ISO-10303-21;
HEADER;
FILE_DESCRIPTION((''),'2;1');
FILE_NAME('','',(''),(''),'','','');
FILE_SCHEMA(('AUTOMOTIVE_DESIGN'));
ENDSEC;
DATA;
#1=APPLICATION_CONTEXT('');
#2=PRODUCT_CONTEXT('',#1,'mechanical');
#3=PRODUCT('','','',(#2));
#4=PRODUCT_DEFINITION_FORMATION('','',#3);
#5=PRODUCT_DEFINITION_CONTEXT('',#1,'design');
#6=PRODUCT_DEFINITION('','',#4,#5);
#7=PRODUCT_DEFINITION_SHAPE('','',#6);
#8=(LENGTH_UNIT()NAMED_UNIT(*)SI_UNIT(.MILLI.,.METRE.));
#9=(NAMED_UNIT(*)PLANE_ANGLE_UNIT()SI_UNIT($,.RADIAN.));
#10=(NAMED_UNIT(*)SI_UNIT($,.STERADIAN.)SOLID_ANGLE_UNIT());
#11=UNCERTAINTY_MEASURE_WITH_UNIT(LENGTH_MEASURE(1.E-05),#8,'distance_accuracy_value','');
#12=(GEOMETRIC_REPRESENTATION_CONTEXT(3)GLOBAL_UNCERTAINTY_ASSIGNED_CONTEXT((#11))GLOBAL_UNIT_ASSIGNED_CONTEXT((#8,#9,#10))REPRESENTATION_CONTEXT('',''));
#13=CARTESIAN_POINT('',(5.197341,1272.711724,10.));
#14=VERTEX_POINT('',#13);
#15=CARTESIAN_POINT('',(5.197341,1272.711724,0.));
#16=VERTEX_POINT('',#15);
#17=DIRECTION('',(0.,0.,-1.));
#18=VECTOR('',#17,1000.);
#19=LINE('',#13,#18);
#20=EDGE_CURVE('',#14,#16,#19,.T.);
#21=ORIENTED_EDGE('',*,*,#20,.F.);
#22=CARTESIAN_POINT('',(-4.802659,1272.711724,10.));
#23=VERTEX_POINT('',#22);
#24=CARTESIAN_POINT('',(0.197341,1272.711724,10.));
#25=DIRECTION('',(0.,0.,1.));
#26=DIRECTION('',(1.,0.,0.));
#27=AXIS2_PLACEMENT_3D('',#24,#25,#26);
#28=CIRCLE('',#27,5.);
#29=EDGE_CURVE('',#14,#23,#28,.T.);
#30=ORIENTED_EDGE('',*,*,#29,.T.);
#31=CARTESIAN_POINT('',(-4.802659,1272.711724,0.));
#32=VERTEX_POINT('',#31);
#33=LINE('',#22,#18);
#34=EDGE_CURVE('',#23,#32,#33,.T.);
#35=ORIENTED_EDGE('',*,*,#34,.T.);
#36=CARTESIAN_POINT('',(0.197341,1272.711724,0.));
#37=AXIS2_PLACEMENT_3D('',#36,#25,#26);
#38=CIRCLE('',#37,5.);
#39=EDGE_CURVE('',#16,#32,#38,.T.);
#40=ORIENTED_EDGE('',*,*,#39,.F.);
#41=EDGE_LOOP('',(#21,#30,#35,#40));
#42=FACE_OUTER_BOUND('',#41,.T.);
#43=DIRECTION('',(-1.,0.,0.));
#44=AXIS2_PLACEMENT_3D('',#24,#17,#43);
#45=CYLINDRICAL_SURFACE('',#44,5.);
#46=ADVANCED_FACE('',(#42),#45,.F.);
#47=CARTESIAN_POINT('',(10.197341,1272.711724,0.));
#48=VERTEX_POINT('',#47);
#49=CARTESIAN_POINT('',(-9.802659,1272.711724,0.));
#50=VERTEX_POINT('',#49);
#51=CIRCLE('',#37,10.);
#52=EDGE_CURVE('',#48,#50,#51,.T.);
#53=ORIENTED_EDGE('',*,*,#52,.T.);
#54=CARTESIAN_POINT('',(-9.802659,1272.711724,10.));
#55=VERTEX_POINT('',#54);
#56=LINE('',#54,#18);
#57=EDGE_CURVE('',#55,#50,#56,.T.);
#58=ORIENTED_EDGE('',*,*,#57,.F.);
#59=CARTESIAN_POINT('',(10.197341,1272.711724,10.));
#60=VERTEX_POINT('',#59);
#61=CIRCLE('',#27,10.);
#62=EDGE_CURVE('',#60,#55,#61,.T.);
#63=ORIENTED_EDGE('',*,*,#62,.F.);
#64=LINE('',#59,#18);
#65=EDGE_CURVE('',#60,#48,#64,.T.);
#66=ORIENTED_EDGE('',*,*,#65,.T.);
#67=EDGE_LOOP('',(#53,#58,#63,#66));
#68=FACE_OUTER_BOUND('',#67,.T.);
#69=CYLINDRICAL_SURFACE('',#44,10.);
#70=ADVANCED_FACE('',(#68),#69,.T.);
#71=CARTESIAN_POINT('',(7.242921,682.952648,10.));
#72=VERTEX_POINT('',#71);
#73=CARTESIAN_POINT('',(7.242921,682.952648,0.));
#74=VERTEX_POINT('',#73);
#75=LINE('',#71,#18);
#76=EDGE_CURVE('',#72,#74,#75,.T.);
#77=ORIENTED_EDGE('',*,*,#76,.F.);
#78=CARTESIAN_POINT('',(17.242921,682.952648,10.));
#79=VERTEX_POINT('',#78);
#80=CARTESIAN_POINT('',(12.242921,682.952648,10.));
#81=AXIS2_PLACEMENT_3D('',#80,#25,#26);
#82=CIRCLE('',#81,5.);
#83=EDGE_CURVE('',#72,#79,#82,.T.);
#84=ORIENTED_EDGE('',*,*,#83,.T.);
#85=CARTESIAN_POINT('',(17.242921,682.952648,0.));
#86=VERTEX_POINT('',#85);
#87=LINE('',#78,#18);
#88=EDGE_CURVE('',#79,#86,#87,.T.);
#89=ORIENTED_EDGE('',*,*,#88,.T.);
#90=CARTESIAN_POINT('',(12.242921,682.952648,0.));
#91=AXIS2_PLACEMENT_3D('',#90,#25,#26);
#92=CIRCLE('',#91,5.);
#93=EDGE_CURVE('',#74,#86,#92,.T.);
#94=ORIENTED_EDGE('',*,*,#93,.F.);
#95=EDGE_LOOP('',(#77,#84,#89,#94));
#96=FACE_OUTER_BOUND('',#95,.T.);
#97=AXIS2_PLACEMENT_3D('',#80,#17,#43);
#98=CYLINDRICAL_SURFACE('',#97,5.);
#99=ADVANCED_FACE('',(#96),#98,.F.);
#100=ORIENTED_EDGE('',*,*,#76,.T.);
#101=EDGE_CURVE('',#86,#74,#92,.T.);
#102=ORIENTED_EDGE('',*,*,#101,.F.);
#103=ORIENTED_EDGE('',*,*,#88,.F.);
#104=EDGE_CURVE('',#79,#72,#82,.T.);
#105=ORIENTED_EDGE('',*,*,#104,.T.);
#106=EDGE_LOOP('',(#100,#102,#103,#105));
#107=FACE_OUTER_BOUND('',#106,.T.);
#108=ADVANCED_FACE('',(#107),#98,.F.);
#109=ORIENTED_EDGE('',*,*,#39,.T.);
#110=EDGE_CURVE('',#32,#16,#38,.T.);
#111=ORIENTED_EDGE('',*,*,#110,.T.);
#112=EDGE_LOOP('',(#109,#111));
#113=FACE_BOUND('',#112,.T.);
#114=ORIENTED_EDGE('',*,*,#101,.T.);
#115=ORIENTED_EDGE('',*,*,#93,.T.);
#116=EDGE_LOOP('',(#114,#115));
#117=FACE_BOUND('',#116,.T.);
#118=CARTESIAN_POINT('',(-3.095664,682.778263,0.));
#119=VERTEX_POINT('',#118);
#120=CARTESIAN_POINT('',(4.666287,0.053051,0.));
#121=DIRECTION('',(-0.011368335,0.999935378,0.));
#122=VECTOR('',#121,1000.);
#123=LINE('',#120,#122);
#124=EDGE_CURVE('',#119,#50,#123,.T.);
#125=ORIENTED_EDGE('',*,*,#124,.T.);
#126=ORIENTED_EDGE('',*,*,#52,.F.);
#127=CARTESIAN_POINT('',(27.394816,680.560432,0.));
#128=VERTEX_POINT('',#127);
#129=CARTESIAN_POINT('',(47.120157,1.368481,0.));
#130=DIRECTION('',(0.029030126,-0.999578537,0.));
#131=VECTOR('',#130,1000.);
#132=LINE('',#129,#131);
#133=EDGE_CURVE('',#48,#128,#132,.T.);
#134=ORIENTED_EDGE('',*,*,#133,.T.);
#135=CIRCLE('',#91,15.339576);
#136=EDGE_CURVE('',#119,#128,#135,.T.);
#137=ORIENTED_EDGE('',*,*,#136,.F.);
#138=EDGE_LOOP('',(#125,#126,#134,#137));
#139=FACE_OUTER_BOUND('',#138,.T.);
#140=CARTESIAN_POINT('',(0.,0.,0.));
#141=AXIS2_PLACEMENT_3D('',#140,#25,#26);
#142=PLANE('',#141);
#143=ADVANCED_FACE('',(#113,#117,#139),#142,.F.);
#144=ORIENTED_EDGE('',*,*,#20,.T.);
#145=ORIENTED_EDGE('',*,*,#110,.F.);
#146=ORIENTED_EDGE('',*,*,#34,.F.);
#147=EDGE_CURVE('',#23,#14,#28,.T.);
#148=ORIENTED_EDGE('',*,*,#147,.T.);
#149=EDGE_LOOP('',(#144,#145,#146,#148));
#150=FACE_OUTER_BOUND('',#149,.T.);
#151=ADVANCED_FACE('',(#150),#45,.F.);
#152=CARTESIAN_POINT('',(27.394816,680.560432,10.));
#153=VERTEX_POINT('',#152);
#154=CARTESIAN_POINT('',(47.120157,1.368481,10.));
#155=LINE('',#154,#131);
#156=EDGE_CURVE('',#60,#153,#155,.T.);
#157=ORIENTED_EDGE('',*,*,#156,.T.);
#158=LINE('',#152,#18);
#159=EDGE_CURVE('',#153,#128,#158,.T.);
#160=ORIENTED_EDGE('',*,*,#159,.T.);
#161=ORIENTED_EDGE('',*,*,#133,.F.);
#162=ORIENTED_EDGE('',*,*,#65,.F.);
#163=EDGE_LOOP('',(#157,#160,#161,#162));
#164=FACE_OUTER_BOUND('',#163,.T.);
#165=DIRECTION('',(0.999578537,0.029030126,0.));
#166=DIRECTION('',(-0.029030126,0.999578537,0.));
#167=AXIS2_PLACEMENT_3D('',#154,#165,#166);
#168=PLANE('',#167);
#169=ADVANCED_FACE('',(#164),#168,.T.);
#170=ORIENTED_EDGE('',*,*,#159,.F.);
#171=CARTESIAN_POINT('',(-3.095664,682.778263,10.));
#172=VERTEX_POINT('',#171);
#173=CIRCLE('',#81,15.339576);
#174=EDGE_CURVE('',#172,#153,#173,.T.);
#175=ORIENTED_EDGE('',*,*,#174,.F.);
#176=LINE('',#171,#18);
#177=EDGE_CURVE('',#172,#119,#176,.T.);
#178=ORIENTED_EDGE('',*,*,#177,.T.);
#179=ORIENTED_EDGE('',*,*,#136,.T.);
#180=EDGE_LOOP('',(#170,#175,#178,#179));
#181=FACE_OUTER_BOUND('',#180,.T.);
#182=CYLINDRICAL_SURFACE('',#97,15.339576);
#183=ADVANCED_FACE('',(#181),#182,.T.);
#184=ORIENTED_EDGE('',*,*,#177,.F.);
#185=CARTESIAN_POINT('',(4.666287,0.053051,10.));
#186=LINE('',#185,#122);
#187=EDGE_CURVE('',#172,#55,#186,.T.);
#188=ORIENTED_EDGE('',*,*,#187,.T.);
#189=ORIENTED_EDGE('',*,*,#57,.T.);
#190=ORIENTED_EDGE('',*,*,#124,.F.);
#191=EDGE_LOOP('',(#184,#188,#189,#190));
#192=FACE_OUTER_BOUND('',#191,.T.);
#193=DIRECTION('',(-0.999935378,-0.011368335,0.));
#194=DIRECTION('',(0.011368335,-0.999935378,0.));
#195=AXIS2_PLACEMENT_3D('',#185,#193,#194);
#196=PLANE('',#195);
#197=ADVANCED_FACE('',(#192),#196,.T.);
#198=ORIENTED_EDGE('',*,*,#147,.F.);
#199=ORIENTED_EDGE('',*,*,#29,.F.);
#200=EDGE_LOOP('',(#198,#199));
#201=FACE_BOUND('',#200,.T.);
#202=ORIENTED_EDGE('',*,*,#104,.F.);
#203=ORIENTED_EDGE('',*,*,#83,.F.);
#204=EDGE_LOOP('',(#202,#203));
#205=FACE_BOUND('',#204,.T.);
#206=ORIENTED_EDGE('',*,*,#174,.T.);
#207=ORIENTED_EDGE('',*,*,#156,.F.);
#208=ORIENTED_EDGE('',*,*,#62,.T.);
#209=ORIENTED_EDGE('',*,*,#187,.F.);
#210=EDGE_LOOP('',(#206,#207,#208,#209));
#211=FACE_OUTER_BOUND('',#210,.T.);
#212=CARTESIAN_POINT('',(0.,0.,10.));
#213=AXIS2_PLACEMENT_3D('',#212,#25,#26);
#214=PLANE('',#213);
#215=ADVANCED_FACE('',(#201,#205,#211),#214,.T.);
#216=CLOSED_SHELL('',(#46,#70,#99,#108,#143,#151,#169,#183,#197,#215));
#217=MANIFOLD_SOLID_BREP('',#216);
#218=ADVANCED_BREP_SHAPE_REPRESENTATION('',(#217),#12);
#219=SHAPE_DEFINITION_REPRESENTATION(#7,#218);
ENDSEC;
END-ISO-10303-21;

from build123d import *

# Parameters (mm, degrees)
SKETCH3_R           = 5
BOSS_EXTRUDE1_DEPTH = 10


with BuildPart() as part:
    # Sketch3 → Boss-Extrude1 (new body)
    # profile 1 of 6: a face of its own
    with BuildSketch(Plane.XY):
        with BuildLine():
            Line((27.39481576, 680.560432475), (27.230443202, 686.220183409))
            Line((27.230443202, 686.220183409), (13.205751534, 1169.124769421))
            ThreePointArc((13.205751534, 1169.124769421), (2.770474558, 1164.302567957), (-8.590118071, 1166.059146344))
            Line((-8.590118071, 1166.059146344), (-3.095663833, 682.778262513))
            ThreePointArc((-3.095663833, 682.778262513), (11.13008439, 667.653491235), (27.39481576, 680.560432475))
        make_face()
        with Locations((12.242921242, 682.952647962)):
            Circle(SKETCH3_R, mode=Mode.SUBTRACT)
    # profile 2 of 6: a face of its own
    with BuildSketch(Plane.XY):
        with BuildLine():
            ThreePointArc((-8.590118071, 1166.059146344), (2.770474558, 1164.302567957), (13.205751534, 1169.124769421))
            Line((13.205751534, 1169.124769421), (10.388282273, 1266.137157238))
            ThreePointArc((10.388282273, 1266.137157238), (5.346882565, 1267.310168836), (0.186416397, 1267.711735959))
            ThreePointArc((0.186416397, 1267.711735959), (-4.824372475, 1267.355069011), (-9.729431527, 1266.270812525))
            Line((-9.729431527, 1266.270812525), (-8.590118071, 1166.059146344))
        make_face()
        with Locations((0, 1184)):
            Circle(SKETCH3_R, mode=Mode.SUBTRACT)
    # profile 3 of 6: a face of its own
    with BuildSketch(Plane.XY):
        with BuildLine():
            ThreePointArc((0.186416397, 1267.711735959), (5.346882565, 1267.310168836), (10.388282273, 1266.137157238))
            Line((10.388282273, 1266.137157238), (10.197341299, 1272.711724024))
            ThreePointArc((10.197341299, 1272.711724024), (9.983454072, 1274.768905783), (9.35094194, 1276.738086563))
            ThreePointArc((9.35094194, 1276.738086563), (4.804919365, 1277.462611062), (0.208267791, 1277.711712085))
            ThreePointArc((0.208267791, 1277.711712085), (3.736736195, 1276.243392718), (5.197341299, 1272.711724024))
            ThreePointArc((5.197341299, 1272.711724024), (3.729010557, 1269.172329689), (0.186416397, 1267.711735959))
        make_face()
    # profile 4 of 6: a face of its own
    with BuildSketch(Plane.XY):
        with BuildLine():
            ThreePointArc((0.208267791, 1277.711712085), (4.804919365, 1277.462611062), (9.35094194, 1276.738086563))
            ThreePointArc((9.35094194, 1276.738086563), (0.219193138, 1282.711700148), (-8.938575282, 1276.778052618))
            ThreePointArc((-8.938575282, 1276.778052618), (-4.38942912, 1277.482702512), (0.208267791, 1277.711712085))
        make_face()
    # profile 5 of 6: a face of its own
    with BuildSketch(Plane.XY):
        with BuildLine():
            ThreePointArc((-9.729431527, 1266.270812525), (-4.824372475, 1267.355069011), (0.186416397, 1267.711735959))
            ThreePointArc((0.186416397, 1267.711735959), (-4.802646764, 1272.722649721), (0.208267791, 1277.711712085))
            ThreePointArc((0.208267791, 1277.711712085), (-4.38942912, 1277.482702512), (-8.938575282, 1276.778052618))
            ThreePointArc((-8.938575282, 1276.778052618), (-9.584252789, 1274.790285328), (-9.802658701, 1272.711724024))
            Line((-9.802658701, 1272.711724024), (-9.80007392, 1272.484372008))
            Line((-9.80007392, 1272.484372008), (-9.729431527, 1266.270812525))
        make_face()
    # profile 6 of 6: a face of its own
    with BuildSketch(Plane.XY):
        with Locations((0, 1184)):
            Circle(SKETCH3_R)
    extrude(amount=BOSS_EXTRUDE1_DEPTH)


solid = part.part
